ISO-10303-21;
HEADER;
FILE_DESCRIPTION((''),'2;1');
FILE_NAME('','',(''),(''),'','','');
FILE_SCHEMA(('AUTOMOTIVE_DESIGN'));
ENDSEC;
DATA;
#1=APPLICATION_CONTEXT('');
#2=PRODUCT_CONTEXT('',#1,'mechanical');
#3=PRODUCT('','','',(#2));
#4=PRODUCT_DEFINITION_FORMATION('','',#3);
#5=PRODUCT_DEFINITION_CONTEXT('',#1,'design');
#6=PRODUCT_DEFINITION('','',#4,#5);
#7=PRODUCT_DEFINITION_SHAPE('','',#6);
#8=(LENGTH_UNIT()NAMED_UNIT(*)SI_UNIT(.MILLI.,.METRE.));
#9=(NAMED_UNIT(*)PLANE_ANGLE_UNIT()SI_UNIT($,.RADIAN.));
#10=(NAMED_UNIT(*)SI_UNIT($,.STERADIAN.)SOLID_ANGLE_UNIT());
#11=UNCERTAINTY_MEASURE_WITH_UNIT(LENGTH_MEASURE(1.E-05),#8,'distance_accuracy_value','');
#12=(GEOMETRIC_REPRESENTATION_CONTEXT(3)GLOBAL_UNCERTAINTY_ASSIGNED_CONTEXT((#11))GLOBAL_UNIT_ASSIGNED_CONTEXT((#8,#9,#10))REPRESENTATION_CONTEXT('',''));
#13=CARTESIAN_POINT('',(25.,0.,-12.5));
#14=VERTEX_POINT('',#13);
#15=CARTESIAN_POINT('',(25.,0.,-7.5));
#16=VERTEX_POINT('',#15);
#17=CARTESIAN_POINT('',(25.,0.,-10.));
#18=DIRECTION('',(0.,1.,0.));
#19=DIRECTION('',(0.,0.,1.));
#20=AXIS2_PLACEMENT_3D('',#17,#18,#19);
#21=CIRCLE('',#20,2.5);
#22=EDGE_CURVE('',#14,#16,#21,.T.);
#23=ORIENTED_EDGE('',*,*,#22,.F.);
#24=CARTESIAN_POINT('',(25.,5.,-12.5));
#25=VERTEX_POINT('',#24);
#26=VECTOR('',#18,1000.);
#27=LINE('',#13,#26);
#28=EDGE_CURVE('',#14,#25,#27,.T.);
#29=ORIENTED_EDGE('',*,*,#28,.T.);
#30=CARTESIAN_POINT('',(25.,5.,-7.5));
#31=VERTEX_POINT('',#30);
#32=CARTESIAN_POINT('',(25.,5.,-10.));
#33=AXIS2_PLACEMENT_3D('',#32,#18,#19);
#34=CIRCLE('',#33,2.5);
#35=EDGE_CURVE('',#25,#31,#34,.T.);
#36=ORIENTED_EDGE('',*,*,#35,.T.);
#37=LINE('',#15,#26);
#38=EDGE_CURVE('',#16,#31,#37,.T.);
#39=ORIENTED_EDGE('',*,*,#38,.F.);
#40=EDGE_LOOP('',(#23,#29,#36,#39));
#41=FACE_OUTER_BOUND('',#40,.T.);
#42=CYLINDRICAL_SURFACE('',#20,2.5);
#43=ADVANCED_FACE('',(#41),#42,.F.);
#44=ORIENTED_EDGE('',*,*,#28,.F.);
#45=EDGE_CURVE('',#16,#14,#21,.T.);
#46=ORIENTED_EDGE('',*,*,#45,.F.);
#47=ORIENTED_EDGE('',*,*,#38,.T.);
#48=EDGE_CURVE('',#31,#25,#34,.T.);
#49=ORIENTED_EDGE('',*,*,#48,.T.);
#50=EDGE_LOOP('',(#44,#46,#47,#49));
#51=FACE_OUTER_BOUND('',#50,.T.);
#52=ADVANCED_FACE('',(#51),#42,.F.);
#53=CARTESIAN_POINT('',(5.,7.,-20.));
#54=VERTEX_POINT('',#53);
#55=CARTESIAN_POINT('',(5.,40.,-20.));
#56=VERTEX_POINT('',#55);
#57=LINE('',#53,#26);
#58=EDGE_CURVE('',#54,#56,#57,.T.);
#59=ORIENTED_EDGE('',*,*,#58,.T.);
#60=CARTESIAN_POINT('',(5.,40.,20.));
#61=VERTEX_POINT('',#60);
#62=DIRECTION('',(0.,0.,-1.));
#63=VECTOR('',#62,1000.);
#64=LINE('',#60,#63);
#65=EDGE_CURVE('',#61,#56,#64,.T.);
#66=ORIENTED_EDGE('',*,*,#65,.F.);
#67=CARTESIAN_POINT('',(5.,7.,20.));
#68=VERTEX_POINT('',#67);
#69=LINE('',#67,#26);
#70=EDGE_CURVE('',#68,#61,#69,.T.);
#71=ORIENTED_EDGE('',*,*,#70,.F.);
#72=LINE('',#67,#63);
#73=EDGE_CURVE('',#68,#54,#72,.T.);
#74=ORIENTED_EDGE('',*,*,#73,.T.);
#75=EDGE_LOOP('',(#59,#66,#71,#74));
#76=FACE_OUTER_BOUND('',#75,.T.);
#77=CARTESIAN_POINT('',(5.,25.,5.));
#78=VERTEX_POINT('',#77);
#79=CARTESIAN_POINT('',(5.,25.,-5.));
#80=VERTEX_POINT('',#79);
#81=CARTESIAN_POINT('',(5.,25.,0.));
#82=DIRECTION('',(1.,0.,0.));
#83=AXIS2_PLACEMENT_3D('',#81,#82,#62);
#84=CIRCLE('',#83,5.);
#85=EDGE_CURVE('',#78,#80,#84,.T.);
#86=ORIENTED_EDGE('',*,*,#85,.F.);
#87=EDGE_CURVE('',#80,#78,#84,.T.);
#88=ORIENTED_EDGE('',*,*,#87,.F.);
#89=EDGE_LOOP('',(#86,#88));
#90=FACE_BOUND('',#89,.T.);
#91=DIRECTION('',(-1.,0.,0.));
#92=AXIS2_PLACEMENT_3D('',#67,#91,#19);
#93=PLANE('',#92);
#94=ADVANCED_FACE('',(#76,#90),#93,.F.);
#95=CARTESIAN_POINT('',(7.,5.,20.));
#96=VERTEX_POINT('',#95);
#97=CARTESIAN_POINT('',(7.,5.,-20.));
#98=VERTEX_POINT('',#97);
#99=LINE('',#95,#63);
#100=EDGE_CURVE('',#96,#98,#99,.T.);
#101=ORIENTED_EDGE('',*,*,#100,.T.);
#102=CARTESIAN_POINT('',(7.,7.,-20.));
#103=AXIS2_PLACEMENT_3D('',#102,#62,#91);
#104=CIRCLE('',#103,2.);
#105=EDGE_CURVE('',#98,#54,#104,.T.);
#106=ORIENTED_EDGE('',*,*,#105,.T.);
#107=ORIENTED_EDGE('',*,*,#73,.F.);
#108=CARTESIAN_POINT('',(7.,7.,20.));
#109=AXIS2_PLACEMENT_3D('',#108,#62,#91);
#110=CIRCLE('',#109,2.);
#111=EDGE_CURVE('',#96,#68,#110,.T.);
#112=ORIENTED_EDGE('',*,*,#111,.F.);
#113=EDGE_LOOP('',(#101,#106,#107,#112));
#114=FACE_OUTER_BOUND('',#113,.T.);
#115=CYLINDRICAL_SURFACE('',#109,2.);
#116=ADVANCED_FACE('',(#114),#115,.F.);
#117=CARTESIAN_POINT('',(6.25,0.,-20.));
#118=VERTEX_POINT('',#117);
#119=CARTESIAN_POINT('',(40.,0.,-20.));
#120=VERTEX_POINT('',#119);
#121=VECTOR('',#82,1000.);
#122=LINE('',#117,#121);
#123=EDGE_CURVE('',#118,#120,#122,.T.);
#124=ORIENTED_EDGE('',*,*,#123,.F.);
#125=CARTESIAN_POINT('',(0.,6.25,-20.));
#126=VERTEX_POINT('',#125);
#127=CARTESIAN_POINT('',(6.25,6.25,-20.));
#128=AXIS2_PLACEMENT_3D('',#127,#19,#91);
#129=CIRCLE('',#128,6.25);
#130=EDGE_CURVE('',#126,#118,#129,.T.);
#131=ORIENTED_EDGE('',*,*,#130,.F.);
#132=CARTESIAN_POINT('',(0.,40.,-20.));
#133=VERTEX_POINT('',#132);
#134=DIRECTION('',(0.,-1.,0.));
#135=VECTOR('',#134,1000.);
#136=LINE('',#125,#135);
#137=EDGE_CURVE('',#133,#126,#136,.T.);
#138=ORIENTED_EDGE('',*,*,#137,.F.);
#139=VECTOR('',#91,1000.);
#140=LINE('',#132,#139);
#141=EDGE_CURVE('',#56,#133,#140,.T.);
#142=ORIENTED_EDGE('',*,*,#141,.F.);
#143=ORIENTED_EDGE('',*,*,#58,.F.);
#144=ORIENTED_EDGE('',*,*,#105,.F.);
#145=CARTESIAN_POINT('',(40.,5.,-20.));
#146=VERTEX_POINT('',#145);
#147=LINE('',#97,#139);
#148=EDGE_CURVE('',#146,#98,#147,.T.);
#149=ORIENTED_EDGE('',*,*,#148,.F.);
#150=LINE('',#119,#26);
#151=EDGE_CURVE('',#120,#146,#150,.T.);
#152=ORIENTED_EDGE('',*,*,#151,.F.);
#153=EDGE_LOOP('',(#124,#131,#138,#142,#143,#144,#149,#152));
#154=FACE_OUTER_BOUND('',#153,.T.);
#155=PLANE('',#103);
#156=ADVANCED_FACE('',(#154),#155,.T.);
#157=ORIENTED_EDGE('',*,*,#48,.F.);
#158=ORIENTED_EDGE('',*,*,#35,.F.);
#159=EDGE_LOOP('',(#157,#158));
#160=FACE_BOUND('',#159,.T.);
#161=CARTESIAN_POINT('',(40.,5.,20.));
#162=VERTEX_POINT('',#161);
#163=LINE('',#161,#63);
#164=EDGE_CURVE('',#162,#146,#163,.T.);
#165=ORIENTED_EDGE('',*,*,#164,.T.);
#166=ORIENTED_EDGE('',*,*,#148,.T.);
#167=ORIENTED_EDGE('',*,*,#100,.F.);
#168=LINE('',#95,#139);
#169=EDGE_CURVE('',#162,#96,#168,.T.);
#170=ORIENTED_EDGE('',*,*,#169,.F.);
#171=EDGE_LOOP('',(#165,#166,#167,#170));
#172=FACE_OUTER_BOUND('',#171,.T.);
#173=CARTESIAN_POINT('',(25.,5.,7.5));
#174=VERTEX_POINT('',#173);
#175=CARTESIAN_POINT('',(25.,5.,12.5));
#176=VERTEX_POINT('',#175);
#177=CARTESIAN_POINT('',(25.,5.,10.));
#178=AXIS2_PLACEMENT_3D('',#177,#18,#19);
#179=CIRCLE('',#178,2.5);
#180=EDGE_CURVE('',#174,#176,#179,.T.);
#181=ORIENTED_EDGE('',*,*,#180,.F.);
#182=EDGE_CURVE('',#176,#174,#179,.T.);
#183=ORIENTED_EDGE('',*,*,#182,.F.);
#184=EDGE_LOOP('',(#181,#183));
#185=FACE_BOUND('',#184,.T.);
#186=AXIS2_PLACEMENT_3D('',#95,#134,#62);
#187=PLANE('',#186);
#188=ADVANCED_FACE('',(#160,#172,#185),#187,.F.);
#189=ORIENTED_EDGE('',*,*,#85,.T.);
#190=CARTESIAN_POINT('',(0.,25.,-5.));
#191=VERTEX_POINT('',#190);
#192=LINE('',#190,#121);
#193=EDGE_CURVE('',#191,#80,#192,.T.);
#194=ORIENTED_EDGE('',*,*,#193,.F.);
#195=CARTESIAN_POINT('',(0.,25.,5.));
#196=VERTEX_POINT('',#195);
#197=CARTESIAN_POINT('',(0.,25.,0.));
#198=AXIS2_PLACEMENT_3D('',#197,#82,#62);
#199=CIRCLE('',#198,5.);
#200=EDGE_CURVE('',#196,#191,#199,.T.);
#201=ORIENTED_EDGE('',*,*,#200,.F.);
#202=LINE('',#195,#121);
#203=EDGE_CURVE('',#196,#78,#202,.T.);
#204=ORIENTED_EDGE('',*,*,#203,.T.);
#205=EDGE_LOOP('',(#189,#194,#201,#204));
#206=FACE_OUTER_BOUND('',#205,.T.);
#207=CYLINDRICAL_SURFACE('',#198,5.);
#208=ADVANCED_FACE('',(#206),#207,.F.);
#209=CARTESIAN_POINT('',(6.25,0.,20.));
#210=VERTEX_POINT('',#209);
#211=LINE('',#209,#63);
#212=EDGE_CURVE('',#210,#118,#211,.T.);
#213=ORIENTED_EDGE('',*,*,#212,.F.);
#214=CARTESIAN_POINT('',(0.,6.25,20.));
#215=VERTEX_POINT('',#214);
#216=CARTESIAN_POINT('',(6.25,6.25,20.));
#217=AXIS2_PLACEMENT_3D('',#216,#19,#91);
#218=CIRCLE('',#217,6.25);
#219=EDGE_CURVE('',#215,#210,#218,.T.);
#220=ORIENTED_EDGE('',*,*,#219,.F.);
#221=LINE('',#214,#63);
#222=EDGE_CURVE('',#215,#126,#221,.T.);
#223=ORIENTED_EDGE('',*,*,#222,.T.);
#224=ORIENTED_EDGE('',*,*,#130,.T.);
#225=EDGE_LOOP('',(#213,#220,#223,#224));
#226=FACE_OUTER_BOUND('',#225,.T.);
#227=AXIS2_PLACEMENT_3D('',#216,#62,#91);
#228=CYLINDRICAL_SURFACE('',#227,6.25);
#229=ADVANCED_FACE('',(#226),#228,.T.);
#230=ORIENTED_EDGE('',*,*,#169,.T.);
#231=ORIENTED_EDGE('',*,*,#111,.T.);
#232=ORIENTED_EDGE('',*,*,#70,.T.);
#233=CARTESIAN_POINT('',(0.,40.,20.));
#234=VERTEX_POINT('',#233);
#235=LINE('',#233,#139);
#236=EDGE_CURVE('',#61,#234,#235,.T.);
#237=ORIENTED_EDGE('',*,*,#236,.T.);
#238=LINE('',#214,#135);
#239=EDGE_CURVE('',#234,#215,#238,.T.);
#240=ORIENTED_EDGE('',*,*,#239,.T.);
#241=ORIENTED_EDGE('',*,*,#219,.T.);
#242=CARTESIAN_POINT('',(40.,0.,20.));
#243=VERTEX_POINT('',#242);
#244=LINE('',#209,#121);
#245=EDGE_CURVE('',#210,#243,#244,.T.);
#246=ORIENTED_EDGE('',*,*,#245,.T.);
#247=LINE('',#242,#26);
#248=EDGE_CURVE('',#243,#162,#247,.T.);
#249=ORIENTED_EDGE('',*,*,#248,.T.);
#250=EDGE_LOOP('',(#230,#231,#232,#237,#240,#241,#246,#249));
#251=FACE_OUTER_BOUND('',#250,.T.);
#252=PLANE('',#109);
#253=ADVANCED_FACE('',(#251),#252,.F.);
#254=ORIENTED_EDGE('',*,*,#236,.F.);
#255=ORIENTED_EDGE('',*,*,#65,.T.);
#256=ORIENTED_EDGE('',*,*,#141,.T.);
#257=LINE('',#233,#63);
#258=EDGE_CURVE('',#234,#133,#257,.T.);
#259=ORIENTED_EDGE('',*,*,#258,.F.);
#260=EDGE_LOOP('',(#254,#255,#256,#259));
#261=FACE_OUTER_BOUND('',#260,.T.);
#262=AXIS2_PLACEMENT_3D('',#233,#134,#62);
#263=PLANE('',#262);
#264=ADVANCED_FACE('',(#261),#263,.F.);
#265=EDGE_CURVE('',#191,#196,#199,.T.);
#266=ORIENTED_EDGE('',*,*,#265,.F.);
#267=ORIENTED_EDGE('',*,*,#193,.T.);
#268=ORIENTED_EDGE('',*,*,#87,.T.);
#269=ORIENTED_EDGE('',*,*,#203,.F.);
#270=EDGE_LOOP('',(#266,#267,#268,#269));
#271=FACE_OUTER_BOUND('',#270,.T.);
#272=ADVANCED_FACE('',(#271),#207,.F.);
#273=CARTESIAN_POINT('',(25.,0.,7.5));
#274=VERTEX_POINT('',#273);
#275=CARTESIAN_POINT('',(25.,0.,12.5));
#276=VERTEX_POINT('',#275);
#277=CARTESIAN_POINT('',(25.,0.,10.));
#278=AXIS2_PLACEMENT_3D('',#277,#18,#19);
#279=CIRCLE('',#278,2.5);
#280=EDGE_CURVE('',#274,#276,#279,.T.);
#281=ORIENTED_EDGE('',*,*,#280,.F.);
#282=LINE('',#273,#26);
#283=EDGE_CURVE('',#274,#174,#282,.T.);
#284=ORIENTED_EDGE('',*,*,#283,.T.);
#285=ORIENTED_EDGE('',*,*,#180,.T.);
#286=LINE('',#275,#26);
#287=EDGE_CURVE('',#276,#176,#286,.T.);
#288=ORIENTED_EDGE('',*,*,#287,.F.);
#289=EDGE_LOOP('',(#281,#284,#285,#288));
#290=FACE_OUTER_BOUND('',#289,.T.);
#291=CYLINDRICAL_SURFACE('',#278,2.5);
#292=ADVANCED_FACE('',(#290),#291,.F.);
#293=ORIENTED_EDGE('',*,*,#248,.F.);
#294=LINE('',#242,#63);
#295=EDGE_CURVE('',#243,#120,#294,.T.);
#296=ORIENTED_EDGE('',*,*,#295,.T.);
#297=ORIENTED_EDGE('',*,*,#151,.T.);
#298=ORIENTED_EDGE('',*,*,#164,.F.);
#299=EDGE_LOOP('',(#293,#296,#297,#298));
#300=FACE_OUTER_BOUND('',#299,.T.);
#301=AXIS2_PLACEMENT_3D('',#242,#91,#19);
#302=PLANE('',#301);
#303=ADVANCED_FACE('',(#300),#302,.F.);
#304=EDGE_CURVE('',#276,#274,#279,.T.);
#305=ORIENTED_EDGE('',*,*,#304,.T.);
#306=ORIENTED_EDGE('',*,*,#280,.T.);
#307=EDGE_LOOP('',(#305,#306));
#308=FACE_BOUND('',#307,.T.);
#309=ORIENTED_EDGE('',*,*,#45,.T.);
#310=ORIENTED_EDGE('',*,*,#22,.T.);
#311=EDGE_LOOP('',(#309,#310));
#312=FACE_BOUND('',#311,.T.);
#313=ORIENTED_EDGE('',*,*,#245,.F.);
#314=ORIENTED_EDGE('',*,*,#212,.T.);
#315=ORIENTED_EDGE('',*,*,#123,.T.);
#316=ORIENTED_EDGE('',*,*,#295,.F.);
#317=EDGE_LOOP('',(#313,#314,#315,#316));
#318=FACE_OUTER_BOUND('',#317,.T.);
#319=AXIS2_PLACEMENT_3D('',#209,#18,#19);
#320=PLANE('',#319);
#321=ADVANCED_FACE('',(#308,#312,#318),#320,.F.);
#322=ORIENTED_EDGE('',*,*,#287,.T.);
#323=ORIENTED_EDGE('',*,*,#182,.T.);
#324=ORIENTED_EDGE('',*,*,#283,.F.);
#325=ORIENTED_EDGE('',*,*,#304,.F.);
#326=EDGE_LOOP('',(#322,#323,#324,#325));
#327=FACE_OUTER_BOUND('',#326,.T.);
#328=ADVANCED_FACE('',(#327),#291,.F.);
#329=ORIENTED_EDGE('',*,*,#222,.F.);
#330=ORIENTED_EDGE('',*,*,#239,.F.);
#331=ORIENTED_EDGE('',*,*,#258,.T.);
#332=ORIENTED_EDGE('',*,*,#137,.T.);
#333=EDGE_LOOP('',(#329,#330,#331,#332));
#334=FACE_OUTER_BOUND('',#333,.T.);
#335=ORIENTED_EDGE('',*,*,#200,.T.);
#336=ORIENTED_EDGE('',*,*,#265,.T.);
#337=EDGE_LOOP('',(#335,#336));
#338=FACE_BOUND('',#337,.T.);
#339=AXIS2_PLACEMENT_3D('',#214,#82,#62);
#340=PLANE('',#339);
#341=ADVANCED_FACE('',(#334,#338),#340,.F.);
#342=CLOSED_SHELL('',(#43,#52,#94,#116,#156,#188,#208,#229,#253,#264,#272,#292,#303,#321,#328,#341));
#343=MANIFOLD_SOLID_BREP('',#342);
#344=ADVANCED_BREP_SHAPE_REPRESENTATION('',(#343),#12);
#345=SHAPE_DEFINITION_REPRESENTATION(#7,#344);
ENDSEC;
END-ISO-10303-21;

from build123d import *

# Parameters (mm, degrees)
L_BRACKET_BODY_DEPTH  = 20
UPRIGHT_HOLE_SKETCH_R = 5
UPRIGHT_HOLE_10_DEPTH = 57.789083458
BASE_HOLES_SKETCH_R   = 2.5
BASE_HOLES_2X_5_DEPTH = 57.789083458


with BuildPart() as part:
    # Bracket Profile Sketch → L-Bracket Body (new, symmetric)
    with BuildSketch(Plane.XY):
        with BuildLine():
            Line((0, 6.25), (0, 40))
            Line((0, 40), (5, 40))
            Line((5, 40), (5, 7))
            ThreePointArc((5, 7), (5.585786438, 5.585786438), (7, 5))
            Line((7, 5), (40, 5))
            Line((40, 5), (40, 0))
            Line((40, 0), (6.25, 0))
            ThreePointArc((6.25, 0), (1.830582618, 1.830582618), (0, 6.25))
        make_face()
    extrude(amount=L_BRACKET_BODY_DEPTH, both=True)

    # Upright Hole Sketch → Upright Hole Ø10 (cut, through all)
    with BuildSketch(Plane(origin=(5, 0, 0), x_dir=(0, 0, -1), z_dir=(1, 0, 0))):
        with Locations((0, 25)):
            Circle(UPRIGHT_HOLE_SKETCH_R)
    extrude(amount=-UPRIGHT_HOLE_10_DEPTH, mode=Mode.SUBTRACT)

    # Base Holes Sketch → Base Holes 2xØ5 (cut, through all)
    with BuildSketch(Plane(origin=(0, 5, 0), x_dir=(1, 0, 0), z_dir=(0, 1, 0))):
        with Locations(Location((25, 10, 0), (0, 0, 270))):
            Circle(BASE_HOLES_SKETCH_R)
        with Locations(Location((25, -10, 0), (0, 0, 270))):
            Circle(BASE_HOLES_SKETCH_R)
    extrude(amount=-BASE_HOLES_2X_5_DEPTH, mode=Mode.SUBTRACT)


solid = part.part
